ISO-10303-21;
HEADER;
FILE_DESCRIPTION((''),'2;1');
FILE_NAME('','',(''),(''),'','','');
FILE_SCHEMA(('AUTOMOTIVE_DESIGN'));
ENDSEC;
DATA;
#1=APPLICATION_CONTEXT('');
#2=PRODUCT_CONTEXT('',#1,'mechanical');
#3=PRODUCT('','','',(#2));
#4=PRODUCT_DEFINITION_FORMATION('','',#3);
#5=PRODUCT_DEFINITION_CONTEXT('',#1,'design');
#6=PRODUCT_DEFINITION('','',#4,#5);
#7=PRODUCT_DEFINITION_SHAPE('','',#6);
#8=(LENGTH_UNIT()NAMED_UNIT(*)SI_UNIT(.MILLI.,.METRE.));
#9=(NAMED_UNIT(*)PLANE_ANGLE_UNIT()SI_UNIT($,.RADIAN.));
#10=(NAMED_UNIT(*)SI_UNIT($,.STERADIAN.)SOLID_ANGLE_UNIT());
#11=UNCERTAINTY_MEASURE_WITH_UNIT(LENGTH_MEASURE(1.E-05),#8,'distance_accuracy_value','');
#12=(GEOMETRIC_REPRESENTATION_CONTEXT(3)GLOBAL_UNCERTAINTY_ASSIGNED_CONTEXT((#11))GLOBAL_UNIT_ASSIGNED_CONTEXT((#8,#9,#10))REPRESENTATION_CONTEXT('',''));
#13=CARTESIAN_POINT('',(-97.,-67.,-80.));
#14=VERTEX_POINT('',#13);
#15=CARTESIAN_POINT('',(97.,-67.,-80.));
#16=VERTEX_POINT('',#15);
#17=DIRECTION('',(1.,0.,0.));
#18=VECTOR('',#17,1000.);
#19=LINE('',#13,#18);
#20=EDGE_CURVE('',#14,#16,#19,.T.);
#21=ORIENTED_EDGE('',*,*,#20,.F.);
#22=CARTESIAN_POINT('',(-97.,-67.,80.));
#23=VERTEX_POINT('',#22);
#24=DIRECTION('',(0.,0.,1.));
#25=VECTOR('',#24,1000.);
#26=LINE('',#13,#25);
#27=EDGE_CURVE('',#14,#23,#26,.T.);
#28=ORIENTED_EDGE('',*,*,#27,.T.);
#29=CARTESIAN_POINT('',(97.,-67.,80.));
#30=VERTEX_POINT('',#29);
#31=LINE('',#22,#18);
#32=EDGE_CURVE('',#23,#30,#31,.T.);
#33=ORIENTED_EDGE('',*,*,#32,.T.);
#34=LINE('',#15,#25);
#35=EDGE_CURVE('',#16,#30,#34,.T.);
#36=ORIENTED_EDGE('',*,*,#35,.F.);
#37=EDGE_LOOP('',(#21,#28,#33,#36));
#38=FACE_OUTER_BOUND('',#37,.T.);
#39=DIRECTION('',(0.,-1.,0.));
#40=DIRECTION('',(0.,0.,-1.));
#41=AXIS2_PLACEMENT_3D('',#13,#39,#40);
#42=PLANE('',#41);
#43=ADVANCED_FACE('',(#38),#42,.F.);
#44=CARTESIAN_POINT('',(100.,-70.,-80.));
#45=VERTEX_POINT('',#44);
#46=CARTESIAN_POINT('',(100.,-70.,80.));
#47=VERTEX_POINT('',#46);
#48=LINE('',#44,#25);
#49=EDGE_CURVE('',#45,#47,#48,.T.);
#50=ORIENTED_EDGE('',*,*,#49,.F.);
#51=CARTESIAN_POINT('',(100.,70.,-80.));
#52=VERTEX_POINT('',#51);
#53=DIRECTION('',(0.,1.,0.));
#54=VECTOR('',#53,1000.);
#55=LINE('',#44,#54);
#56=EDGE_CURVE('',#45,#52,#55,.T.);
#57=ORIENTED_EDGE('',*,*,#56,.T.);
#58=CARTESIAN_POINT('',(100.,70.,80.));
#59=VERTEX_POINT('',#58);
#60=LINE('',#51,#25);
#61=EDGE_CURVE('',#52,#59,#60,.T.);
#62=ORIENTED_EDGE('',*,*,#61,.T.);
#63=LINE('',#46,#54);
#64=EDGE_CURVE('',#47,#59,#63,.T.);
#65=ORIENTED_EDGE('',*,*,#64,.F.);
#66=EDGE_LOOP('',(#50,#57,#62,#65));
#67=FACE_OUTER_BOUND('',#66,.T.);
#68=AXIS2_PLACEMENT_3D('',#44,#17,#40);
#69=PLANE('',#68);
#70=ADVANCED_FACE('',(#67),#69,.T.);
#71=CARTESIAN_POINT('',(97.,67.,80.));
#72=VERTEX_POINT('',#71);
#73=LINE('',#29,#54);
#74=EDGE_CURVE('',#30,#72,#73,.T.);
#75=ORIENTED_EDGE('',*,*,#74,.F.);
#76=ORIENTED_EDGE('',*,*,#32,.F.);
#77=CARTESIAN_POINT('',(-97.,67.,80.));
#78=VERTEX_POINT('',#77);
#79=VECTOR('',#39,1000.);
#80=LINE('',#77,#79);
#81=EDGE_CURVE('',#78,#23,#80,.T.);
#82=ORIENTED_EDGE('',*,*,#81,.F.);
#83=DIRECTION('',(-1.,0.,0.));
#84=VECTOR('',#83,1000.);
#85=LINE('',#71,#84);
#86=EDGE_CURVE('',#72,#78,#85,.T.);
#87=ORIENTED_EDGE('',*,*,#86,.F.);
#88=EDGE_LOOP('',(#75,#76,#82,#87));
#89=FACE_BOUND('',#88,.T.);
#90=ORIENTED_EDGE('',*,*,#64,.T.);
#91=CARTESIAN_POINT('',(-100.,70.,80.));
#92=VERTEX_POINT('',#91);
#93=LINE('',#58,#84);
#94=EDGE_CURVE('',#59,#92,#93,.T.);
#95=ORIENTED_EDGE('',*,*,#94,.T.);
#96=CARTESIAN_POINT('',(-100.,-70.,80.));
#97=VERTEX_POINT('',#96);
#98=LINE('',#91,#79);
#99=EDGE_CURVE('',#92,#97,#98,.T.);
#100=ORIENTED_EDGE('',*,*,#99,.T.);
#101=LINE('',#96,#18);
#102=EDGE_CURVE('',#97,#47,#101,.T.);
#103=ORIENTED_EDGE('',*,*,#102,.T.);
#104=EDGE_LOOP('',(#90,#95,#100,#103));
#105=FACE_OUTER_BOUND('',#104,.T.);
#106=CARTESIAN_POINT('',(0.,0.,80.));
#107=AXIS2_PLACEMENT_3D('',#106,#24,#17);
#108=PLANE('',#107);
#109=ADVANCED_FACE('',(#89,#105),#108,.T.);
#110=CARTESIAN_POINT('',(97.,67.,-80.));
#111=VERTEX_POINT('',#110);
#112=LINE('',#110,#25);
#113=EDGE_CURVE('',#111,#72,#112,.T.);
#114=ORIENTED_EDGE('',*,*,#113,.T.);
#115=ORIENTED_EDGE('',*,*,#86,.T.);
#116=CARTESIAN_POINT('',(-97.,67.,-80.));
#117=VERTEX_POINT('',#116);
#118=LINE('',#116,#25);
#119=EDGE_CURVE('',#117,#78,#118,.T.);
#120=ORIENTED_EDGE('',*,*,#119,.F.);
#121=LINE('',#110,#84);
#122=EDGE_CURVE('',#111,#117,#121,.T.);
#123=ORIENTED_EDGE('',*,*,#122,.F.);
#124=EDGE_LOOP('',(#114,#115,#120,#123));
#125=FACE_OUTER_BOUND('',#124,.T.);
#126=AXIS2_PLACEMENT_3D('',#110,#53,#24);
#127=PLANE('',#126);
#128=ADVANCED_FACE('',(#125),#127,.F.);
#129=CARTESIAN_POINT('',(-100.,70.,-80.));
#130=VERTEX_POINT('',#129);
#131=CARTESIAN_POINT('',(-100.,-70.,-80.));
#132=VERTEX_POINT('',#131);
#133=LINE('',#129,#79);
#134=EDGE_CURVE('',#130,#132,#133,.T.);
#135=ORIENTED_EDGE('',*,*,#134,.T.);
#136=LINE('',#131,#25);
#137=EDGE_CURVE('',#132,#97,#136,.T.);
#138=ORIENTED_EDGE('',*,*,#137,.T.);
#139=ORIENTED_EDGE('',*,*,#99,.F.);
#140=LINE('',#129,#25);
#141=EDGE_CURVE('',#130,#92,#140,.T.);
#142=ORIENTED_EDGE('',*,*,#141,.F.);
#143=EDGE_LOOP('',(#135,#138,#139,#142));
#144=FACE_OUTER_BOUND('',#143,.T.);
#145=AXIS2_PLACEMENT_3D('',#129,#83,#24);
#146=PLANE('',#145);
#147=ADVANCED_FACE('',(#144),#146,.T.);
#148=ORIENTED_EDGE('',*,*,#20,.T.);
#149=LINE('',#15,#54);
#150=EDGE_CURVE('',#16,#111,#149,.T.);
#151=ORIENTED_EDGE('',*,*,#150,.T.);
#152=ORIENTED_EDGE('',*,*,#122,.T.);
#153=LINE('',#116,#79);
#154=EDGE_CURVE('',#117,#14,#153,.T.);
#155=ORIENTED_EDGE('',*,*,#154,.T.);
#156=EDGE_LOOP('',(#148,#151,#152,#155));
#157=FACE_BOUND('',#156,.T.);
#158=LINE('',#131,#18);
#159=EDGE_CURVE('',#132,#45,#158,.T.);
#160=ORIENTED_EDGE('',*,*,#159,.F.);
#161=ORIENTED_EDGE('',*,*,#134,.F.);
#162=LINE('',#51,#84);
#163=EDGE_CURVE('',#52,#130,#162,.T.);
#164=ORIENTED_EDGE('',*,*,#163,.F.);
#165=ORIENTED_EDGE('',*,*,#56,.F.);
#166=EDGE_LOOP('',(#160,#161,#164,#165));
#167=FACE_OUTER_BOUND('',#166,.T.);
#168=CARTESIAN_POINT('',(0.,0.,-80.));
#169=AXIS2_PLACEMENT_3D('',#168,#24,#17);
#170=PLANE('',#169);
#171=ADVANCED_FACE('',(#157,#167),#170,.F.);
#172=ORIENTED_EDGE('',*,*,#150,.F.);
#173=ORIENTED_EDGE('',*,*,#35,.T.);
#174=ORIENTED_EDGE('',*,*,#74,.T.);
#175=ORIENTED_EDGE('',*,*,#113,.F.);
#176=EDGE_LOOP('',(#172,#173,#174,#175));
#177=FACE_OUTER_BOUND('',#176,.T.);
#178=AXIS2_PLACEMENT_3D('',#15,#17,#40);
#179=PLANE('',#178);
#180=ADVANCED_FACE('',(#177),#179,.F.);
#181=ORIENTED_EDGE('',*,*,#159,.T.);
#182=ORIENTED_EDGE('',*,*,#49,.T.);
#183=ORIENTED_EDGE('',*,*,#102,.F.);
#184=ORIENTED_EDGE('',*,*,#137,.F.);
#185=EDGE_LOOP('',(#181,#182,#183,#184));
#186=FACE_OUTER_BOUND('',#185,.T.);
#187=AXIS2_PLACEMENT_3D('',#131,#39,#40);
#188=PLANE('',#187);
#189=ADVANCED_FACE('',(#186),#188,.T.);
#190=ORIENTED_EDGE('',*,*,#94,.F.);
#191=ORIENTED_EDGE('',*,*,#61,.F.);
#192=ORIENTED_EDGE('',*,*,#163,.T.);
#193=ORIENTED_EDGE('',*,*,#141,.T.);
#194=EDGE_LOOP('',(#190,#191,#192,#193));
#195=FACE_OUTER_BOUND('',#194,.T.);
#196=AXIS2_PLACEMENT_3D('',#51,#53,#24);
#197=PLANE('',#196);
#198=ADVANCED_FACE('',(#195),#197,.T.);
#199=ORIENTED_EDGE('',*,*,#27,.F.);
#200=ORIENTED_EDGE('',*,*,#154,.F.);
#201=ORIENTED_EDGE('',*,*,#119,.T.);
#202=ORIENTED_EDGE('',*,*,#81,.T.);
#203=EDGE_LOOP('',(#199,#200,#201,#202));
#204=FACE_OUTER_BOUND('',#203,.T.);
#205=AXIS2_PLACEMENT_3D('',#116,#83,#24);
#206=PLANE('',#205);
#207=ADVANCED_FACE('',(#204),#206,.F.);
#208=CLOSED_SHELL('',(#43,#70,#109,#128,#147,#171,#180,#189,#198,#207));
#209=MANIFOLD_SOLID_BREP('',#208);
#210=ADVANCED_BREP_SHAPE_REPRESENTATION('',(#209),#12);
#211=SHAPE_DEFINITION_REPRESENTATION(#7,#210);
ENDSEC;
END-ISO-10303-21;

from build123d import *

# Parameters (mm, degrees)
SKETCH_1_W      = 200
SKETCH_1_H      = 140
SKETCH_1_W_2    = 194
SKETCH_1_H_2    = 134
EXTRUDE_1_DEPTH = 80


with BuildPart() as part:
    # 草图1 → 凸台-拉伸1 (new, symmetric)
    with BuildSketch(Plane.XY):
        Rectangle(SKETCH_1_W, SKETCH_1_H)
        Rectangle(SKETCH_1_W_2, SKETCH_1_H_2, mode=Mode.SUBTRACT)
    extrude(amount=EXTRUDE_1_DEPTH, both=True)


solid = part.part
